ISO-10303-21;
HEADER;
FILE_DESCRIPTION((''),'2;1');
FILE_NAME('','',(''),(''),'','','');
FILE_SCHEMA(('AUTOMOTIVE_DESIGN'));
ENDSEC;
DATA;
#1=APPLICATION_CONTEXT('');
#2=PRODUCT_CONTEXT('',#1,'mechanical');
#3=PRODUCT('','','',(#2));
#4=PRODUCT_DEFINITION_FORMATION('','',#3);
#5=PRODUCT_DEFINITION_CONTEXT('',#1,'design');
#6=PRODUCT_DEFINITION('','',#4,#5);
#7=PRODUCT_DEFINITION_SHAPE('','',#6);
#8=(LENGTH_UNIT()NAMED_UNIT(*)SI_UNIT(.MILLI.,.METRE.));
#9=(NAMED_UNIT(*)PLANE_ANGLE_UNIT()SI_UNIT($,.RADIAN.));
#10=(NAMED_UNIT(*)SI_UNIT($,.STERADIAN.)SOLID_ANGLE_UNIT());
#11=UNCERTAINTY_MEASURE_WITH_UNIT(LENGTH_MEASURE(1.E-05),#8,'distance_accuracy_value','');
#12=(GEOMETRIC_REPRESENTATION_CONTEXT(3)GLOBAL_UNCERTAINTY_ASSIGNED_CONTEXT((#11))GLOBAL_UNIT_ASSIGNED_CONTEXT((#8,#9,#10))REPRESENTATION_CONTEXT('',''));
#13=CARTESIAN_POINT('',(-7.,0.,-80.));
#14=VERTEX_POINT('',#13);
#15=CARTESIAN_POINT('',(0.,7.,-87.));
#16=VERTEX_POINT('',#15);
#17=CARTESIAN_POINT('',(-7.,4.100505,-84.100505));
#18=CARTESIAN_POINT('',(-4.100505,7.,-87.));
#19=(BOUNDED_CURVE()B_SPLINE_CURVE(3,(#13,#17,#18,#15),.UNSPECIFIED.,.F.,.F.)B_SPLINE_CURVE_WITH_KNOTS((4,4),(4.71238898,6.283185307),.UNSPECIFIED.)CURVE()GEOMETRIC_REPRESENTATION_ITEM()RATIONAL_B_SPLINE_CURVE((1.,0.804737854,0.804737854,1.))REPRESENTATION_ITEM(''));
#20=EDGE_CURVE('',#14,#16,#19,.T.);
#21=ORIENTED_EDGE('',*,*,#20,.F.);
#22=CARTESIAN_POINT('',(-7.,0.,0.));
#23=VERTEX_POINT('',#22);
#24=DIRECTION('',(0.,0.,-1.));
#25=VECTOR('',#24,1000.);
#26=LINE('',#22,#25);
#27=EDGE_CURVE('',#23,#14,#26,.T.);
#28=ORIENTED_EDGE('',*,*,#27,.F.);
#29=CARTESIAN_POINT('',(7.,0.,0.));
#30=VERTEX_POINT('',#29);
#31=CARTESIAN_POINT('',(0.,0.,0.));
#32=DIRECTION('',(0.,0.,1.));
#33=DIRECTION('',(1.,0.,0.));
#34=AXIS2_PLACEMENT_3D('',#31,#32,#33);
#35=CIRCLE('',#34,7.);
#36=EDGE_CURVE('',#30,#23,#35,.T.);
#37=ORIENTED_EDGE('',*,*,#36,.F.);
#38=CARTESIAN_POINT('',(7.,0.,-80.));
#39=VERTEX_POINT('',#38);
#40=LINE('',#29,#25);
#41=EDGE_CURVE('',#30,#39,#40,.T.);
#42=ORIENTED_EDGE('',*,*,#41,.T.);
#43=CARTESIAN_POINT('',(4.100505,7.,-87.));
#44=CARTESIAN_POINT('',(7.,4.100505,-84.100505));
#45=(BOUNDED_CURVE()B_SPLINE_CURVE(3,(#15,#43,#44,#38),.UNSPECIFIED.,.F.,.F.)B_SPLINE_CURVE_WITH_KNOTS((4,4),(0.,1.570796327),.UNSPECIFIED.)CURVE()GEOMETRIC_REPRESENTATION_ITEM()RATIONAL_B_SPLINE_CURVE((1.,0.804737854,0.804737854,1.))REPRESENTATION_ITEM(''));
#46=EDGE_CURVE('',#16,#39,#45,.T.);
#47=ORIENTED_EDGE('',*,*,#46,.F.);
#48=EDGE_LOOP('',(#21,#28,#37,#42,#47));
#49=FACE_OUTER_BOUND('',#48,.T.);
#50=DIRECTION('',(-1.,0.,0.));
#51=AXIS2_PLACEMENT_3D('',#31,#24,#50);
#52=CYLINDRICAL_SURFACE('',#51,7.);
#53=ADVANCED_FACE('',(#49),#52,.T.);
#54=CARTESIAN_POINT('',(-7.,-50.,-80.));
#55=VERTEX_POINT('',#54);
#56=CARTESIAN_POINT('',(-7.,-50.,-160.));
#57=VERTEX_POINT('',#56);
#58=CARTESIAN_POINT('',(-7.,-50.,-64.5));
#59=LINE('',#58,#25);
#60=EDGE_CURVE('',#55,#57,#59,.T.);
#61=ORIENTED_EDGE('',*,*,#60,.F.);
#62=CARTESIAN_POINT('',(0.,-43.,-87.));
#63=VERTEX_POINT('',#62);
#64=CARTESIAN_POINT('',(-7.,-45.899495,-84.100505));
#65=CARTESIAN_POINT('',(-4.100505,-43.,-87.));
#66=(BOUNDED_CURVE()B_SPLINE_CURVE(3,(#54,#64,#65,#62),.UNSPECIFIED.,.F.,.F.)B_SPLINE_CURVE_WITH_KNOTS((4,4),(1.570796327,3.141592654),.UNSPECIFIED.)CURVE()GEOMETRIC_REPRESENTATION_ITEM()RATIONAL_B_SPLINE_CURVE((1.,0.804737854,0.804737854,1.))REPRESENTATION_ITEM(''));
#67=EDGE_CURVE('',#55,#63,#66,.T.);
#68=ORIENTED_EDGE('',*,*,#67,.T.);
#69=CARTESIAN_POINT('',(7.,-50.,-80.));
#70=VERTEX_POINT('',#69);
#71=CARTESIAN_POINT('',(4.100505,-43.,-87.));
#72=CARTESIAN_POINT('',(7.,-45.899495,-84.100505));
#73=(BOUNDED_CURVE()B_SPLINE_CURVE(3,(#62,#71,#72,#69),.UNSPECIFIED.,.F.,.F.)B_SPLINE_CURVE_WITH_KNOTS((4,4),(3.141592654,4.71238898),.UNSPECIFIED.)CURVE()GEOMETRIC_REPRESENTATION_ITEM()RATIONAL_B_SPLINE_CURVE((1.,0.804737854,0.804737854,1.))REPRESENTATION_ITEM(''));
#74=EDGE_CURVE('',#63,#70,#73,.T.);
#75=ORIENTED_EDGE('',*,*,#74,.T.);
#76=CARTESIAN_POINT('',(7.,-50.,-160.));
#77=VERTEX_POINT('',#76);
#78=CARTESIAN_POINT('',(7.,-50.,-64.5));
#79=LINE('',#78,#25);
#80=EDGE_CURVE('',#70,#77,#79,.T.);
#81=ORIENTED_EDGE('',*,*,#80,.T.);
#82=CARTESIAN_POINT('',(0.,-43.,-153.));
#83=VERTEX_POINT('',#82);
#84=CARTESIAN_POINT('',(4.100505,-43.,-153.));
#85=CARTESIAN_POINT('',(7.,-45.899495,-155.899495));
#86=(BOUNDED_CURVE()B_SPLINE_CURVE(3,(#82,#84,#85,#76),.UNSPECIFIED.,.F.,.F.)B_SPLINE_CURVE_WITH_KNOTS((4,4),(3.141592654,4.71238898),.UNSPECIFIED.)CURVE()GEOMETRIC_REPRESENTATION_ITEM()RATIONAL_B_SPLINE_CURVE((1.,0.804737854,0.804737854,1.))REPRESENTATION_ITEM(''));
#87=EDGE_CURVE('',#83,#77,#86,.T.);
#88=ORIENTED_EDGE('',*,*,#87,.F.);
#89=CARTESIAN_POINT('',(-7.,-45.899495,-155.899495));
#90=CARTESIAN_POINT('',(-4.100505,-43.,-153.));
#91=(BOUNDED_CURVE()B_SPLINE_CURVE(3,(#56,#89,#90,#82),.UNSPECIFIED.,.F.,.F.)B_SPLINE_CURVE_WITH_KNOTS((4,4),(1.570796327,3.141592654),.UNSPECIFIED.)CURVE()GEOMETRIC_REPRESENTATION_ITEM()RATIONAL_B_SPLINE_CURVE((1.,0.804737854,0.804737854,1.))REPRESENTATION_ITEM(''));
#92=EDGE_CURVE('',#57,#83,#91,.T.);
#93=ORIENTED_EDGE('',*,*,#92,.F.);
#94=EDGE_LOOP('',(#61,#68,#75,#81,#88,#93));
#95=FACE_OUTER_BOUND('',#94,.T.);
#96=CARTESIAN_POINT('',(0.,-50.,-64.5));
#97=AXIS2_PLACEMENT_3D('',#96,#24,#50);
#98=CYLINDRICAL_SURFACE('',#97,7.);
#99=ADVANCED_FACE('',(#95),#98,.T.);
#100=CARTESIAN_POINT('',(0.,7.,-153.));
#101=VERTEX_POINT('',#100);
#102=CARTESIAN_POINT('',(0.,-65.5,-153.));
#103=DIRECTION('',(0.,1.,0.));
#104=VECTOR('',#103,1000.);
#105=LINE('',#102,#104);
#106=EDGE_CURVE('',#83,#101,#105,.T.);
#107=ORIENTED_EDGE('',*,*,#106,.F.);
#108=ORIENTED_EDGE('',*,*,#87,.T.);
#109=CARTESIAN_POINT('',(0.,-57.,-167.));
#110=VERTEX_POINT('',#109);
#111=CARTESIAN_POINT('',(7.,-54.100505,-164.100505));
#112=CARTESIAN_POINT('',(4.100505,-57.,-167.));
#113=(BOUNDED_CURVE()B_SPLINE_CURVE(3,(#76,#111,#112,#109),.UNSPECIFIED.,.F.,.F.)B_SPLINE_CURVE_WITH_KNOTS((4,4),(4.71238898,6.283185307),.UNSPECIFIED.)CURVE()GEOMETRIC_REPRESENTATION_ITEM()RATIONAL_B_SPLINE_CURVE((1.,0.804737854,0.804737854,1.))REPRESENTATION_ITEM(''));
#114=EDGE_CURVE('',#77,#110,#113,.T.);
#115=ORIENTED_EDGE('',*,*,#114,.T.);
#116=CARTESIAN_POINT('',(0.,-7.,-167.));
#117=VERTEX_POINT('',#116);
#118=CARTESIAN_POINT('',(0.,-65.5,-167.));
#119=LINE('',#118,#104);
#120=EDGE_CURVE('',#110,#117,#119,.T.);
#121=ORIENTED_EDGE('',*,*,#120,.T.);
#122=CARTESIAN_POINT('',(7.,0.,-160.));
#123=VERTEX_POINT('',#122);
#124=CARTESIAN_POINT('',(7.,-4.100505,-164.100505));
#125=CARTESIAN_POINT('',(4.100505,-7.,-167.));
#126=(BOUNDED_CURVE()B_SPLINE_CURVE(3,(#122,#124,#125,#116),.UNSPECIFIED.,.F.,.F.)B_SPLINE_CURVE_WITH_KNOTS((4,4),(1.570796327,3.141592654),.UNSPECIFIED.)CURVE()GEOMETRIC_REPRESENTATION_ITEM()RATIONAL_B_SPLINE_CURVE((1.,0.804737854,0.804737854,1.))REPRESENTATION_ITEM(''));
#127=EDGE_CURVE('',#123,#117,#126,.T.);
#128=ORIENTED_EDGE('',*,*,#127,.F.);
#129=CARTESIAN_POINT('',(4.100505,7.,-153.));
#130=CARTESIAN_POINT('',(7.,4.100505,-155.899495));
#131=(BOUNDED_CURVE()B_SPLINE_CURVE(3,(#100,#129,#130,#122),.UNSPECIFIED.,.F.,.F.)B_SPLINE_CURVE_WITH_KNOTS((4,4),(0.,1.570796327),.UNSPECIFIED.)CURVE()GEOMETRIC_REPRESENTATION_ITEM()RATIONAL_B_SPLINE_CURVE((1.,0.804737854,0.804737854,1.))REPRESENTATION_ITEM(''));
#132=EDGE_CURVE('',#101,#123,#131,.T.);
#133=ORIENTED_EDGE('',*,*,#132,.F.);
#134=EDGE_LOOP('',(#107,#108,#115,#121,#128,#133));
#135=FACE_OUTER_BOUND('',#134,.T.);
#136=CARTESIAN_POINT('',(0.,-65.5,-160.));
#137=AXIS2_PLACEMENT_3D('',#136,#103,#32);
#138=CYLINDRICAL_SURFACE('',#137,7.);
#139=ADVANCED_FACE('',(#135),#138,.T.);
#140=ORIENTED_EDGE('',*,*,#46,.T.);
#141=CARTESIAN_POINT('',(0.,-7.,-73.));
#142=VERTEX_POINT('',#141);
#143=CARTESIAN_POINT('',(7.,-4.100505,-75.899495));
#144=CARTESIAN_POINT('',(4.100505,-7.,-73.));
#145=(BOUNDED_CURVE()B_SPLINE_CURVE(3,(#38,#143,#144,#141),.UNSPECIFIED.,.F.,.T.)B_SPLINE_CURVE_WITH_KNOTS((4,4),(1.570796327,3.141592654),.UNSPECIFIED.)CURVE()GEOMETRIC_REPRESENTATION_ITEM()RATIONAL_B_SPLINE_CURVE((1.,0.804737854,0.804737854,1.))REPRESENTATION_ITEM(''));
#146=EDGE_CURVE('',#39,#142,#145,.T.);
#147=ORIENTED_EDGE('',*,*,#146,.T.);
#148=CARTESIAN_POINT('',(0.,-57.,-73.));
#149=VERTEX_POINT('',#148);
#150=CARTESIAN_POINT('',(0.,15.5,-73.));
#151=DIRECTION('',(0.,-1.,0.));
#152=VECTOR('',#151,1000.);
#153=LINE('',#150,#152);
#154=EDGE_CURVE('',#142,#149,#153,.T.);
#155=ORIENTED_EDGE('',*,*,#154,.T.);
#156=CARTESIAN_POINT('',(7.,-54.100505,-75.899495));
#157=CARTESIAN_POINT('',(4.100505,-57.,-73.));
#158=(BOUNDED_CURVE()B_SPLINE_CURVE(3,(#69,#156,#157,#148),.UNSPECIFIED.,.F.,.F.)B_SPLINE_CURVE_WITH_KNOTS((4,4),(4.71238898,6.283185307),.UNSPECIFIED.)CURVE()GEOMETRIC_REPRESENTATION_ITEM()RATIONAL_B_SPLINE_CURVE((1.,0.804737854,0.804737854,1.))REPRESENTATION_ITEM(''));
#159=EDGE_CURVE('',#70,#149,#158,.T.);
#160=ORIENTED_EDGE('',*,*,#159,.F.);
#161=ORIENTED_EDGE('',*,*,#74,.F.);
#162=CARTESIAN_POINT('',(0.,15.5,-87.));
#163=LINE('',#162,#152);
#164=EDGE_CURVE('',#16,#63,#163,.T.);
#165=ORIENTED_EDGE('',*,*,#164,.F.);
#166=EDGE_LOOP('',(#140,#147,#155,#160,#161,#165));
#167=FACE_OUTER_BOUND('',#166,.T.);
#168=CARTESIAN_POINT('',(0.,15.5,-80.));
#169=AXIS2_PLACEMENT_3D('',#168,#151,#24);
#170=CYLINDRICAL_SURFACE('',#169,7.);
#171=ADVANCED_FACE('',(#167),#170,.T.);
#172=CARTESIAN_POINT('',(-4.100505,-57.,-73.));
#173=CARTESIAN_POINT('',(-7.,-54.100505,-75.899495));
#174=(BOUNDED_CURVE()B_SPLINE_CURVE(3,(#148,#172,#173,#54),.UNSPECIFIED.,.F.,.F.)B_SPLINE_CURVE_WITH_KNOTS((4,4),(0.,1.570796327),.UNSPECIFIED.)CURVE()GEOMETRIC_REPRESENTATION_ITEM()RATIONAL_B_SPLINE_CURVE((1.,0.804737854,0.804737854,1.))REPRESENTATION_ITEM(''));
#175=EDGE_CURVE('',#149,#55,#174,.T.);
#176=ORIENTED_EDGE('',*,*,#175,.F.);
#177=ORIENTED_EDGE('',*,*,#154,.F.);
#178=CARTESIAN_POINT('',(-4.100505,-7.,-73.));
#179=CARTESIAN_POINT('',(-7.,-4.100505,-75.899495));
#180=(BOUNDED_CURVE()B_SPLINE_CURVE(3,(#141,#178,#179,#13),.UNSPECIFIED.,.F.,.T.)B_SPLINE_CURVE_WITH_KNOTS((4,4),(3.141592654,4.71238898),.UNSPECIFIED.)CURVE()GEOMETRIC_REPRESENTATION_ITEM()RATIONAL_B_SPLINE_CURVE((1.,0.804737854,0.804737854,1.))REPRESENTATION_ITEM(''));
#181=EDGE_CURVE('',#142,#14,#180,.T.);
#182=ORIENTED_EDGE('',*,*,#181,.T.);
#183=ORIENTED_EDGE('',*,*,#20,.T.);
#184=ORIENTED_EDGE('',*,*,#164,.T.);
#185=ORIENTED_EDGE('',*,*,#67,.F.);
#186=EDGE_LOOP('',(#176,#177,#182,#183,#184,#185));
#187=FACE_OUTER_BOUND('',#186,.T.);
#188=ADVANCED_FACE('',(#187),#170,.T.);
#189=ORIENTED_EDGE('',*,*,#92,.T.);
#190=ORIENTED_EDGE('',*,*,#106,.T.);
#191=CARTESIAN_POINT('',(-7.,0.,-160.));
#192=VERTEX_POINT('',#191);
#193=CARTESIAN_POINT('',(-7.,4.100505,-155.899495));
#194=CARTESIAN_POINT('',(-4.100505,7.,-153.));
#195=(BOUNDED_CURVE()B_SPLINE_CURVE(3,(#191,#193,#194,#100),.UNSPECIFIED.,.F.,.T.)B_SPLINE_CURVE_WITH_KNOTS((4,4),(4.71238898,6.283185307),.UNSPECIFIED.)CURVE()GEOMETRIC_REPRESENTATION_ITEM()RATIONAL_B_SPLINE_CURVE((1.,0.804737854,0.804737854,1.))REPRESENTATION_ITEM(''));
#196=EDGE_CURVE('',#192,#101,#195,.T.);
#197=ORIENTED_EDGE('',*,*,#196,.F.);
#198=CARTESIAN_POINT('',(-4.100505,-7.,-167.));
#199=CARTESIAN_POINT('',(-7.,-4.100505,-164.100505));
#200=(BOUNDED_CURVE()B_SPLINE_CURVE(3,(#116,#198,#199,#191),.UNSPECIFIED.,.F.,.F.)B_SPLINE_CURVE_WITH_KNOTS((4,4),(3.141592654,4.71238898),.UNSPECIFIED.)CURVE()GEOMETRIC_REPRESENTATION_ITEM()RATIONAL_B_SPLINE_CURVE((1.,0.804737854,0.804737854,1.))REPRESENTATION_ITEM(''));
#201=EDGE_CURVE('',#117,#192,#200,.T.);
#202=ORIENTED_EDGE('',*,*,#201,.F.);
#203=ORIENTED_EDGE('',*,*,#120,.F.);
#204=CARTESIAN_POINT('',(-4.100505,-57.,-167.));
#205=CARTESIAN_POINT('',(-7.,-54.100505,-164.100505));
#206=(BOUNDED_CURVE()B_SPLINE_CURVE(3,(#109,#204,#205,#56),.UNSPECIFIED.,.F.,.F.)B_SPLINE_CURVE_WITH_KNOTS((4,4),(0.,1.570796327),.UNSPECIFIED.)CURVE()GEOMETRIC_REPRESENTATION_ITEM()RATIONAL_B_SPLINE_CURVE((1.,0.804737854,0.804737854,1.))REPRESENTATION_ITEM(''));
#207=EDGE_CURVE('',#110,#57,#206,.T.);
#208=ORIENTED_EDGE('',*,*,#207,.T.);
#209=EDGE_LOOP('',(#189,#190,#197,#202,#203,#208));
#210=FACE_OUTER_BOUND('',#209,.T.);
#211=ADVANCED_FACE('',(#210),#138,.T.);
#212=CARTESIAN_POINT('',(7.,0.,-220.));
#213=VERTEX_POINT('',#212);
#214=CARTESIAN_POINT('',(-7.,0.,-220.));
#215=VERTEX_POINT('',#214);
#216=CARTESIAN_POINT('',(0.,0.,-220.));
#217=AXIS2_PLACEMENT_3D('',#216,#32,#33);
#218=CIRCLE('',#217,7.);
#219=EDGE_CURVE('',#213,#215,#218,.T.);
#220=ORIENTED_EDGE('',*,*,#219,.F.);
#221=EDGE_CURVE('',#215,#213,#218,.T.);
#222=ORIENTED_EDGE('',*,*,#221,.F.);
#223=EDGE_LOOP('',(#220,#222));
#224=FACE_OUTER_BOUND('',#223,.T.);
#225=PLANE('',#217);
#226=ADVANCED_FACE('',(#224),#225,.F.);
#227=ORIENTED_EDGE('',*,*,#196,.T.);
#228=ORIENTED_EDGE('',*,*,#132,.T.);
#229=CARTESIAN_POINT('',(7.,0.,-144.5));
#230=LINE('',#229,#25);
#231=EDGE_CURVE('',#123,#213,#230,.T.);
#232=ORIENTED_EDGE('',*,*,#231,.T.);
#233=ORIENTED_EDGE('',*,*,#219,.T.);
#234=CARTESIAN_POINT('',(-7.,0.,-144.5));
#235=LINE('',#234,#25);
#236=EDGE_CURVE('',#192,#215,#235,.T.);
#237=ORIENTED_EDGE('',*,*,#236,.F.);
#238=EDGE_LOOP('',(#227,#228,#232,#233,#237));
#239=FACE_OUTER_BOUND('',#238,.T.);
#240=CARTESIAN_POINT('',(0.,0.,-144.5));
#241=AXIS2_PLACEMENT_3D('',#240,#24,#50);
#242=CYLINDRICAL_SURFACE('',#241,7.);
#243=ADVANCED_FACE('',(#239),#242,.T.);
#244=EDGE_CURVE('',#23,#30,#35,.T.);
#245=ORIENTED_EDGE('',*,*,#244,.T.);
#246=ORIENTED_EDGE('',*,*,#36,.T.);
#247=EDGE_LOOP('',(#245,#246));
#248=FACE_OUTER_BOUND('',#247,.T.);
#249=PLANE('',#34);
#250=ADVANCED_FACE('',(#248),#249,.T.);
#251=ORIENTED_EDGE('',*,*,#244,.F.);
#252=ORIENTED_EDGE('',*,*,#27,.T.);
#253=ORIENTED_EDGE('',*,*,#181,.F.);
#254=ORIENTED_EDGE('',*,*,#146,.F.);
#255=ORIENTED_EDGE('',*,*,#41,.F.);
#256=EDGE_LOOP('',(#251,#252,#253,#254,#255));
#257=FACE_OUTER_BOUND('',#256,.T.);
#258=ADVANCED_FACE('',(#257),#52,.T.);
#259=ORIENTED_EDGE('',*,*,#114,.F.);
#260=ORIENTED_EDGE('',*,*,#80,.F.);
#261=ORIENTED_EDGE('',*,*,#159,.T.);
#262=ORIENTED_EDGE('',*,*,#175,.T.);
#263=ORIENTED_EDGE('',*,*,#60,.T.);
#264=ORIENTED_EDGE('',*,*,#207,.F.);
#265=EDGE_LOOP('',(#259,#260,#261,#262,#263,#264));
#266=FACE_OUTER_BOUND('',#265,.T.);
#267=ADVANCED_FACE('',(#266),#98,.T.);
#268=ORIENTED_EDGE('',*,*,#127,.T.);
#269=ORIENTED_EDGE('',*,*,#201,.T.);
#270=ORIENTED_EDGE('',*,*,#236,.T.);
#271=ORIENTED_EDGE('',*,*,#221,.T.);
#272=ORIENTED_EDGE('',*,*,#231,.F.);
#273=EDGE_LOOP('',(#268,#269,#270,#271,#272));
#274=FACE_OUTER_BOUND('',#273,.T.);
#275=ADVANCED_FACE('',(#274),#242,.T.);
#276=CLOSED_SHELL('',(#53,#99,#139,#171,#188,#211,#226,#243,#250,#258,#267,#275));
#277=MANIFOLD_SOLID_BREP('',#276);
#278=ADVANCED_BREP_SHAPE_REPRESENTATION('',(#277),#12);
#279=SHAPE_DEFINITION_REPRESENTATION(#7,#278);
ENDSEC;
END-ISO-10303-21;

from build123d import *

# Parameters (mm, degrees)
SKETCH_1_R = 7


with BuildPart() as part:
    # 扫描1: sweep along a path in 草图3
    with BuildLine(Plane(origin=(0, 0, 0), x_dir=(0, 0, -1), z_dir=(1, 0, 0))) as sweep_1_path:
        Line((0, 0), (80, 0))
        Line((80, 0), (80, -50))
        Line((80, -50), (160, -50))
        Line((160, -50), (160, 0))
        Line((160, 0), (220, 0))
    # 草图1 → 扫描1 (sweep)
    with BuildSketch(Plane.XY):
        Circle(SKETCH_1_R)
    sweep(path=sweep_1_path.line, transition=Transition.RIGHT)


solid = part.part
